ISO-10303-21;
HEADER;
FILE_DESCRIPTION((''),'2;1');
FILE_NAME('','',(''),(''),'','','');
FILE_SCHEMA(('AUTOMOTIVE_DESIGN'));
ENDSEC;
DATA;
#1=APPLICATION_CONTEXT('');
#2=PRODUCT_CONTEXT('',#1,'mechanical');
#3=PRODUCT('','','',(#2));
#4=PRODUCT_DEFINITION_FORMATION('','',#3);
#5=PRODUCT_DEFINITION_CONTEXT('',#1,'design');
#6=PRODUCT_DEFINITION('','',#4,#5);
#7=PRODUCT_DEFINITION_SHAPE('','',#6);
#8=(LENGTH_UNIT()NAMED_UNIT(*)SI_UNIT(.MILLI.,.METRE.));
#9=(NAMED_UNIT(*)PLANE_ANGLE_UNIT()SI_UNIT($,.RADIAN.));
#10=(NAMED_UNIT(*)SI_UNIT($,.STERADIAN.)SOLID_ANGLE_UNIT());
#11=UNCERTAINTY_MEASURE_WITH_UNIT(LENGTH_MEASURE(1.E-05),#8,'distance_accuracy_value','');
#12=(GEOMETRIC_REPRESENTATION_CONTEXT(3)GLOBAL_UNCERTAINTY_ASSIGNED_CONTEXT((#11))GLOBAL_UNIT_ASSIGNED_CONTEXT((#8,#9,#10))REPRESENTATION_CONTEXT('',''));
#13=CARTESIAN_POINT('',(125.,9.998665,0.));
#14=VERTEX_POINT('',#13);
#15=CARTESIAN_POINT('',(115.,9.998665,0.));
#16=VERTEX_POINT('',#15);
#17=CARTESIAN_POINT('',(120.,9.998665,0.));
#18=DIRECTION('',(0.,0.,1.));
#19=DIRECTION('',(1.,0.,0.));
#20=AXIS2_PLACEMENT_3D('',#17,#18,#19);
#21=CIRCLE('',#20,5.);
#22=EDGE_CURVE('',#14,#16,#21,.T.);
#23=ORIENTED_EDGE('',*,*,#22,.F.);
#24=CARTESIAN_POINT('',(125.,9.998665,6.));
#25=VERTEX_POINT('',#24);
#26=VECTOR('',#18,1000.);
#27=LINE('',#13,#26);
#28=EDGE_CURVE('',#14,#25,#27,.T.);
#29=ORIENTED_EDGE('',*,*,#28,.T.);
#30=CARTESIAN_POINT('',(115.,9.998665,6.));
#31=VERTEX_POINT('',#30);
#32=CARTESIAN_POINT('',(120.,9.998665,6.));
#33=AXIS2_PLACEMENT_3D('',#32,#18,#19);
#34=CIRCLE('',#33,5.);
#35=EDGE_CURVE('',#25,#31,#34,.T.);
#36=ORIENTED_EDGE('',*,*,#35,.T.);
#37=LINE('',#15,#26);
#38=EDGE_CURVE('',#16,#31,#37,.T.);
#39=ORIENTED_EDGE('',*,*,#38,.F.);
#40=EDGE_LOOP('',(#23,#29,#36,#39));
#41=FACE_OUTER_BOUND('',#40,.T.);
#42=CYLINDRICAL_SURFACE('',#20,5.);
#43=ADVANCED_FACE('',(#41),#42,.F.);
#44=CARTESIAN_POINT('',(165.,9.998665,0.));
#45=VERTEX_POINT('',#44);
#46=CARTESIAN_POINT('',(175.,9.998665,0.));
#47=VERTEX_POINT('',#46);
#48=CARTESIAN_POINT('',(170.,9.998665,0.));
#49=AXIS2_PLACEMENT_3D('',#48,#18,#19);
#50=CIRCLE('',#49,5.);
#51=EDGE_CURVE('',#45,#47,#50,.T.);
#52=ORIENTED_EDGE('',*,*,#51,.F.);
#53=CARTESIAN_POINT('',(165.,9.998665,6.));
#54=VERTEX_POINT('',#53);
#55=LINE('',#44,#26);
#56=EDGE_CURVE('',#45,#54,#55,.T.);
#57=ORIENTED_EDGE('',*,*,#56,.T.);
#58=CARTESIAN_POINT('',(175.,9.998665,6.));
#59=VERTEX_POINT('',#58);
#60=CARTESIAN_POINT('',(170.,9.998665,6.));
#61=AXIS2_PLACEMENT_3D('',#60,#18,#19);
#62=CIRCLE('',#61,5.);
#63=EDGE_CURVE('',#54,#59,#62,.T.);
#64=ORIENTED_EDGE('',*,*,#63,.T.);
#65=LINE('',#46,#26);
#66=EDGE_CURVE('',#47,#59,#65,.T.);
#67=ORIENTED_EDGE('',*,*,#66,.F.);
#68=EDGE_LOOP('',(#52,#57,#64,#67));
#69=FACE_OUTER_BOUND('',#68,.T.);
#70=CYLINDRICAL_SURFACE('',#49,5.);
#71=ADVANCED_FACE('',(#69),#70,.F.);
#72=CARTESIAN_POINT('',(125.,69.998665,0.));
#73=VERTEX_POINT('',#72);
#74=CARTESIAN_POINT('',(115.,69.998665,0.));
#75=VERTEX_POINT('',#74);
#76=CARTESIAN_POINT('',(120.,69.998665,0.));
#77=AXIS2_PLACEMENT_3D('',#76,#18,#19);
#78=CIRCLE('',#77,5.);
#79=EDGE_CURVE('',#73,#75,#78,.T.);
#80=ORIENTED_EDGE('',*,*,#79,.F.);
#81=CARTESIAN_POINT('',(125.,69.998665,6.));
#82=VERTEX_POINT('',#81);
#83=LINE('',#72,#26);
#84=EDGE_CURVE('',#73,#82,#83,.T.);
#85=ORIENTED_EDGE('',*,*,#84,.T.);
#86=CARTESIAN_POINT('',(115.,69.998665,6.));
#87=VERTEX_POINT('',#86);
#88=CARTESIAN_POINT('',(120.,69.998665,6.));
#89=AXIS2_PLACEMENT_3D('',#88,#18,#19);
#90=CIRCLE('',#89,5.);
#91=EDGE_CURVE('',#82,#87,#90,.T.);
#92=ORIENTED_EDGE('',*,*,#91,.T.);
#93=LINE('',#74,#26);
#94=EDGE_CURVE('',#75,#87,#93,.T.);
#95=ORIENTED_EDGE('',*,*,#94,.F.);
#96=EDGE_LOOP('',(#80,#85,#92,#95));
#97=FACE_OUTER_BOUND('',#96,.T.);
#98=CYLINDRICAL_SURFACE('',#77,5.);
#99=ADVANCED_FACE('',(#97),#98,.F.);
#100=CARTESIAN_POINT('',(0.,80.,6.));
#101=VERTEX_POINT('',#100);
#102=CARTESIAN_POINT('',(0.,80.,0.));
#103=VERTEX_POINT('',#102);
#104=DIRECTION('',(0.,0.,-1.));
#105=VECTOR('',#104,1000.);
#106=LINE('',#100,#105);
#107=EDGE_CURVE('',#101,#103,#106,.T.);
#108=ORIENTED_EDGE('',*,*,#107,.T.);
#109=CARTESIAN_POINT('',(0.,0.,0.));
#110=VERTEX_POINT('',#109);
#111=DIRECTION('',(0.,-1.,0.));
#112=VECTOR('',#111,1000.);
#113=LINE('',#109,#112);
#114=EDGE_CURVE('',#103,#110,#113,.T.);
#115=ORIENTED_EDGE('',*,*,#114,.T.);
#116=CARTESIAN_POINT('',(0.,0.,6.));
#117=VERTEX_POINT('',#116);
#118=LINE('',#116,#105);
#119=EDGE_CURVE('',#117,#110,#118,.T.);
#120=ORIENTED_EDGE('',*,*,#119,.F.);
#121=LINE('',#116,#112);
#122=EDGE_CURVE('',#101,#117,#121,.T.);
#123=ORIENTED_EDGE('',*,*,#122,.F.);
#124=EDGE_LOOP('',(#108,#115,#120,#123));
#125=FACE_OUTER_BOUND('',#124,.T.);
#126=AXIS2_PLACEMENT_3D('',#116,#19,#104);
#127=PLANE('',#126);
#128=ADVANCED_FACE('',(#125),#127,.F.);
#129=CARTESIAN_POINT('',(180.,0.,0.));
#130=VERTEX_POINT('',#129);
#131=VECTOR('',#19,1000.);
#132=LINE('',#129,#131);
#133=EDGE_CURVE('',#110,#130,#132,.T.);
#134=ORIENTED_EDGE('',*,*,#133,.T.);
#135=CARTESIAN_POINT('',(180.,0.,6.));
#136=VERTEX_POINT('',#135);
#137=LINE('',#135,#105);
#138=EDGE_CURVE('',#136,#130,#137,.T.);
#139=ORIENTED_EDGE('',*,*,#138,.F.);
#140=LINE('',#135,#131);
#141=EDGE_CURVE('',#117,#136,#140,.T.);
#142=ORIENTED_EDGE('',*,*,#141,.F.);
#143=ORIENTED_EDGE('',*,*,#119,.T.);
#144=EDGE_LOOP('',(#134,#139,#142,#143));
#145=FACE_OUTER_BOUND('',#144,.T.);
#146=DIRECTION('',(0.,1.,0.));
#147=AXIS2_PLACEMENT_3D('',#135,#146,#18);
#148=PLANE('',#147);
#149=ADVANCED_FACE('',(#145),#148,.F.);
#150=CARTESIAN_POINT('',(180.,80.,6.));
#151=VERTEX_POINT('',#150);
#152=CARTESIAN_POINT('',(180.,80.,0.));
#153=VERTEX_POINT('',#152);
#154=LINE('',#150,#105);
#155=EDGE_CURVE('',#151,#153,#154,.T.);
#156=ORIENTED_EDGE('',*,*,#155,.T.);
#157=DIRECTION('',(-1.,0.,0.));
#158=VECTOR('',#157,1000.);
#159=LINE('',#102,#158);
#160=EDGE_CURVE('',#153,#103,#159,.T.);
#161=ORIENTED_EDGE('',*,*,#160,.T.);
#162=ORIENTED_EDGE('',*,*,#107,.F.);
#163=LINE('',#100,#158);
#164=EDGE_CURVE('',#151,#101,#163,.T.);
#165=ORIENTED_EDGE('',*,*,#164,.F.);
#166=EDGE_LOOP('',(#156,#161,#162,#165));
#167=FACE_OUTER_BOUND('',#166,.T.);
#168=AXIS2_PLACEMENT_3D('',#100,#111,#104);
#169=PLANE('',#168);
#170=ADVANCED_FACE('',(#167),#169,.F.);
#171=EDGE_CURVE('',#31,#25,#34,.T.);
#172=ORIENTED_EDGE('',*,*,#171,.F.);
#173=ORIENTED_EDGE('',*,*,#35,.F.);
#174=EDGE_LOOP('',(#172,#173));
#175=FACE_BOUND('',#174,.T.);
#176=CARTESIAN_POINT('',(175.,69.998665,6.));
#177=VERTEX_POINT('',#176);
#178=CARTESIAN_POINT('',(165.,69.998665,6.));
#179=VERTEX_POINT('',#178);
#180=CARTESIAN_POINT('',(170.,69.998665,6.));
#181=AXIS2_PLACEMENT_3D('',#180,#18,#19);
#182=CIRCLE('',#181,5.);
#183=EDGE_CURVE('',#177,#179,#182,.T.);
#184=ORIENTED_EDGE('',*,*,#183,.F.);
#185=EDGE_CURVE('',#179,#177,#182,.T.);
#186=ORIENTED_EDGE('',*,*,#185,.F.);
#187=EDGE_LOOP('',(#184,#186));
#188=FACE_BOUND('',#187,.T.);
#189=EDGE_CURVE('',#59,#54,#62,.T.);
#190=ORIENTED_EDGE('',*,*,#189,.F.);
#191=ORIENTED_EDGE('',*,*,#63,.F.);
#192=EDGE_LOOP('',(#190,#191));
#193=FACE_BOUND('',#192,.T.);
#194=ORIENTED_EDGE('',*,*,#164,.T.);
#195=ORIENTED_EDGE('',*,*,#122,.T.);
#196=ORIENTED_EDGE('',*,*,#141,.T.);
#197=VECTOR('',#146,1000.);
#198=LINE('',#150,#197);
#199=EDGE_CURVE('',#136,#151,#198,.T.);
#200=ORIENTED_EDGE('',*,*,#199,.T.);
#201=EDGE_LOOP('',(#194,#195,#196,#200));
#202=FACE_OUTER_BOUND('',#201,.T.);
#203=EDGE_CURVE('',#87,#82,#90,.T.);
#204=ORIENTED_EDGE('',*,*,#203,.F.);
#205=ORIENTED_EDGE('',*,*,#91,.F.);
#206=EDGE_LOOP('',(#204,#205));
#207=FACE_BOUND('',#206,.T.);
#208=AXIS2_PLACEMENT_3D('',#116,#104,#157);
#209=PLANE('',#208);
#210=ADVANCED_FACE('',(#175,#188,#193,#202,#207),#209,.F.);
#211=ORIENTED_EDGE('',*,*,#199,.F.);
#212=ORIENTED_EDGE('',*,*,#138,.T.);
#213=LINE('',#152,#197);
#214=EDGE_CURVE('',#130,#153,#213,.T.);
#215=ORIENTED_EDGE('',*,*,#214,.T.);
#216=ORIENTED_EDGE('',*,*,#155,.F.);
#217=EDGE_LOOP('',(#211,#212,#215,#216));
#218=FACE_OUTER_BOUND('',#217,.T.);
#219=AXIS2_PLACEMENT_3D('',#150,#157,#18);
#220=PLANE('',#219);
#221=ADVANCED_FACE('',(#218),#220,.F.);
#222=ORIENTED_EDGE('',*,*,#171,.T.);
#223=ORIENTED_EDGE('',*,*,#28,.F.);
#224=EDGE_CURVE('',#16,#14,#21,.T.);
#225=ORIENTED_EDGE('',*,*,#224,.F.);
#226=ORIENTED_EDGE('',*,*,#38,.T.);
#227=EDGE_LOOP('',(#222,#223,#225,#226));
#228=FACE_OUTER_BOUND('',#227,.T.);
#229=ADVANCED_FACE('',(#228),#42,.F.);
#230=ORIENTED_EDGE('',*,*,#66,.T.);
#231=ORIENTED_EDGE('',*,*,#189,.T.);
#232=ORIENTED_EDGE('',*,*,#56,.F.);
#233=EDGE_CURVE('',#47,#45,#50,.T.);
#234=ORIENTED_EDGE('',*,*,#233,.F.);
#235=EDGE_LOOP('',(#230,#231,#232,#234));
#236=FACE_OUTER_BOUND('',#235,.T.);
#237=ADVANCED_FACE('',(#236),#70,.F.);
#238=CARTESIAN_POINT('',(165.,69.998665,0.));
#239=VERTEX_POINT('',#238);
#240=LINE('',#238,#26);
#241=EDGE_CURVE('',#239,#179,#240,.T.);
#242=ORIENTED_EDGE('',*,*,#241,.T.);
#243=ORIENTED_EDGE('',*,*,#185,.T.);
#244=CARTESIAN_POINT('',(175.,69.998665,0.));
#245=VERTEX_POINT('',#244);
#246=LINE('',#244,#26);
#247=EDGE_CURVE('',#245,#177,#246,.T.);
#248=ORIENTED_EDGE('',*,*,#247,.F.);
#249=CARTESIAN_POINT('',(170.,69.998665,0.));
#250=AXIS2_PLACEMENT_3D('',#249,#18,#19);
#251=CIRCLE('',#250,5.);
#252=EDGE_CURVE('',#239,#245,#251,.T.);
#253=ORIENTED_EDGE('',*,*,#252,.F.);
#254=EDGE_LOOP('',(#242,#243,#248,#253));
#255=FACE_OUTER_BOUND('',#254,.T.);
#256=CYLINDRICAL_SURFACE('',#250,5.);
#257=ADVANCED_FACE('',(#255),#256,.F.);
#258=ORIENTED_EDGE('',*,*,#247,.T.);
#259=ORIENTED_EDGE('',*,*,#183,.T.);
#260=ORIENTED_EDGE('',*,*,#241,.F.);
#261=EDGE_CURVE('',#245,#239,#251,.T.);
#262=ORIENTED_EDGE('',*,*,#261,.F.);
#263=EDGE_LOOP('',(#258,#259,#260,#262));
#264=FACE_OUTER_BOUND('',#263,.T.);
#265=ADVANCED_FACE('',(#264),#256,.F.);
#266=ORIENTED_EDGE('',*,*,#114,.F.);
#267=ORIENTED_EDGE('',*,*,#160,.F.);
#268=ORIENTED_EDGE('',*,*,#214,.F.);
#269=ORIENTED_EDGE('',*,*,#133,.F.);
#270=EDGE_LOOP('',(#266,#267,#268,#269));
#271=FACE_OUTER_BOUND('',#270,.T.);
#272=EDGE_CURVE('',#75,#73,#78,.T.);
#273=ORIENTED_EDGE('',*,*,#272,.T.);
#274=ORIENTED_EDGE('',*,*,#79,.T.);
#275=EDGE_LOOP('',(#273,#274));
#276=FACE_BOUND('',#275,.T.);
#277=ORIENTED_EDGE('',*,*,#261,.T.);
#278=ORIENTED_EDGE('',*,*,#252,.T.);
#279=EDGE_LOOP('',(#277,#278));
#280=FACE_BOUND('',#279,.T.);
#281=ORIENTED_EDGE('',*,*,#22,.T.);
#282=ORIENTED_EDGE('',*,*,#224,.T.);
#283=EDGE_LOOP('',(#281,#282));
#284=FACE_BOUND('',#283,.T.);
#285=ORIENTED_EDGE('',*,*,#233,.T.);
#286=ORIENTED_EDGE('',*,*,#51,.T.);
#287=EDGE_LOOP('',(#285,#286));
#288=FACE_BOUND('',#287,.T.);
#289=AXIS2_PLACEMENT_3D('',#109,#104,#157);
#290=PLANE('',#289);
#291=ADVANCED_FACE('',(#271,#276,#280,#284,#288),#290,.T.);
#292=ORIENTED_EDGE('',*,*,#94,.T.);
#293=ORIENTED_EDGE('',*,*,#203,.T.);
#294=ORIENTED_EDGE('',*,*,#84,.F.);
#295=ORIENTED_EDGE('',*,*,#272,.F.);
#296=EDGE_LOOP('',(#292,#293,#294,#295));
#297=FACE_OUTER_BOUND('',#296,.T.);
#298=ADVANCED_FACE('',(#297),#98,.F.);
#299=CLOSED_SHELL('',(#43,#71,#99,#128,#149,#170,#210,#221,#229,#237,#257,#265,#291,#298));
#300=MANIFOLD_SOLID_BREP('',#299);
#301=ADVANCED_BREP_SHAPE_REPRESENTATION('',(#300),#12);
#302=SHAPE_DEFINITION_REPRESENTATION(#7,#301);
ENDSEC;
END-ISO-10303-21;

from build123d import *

# Parameters (mm, degrees)
SKETCH_1_W          = 180
SKETCH_1_H          = 80
EXTRUDE_1_DEPTH     = 6
SKETCH_2_R          = 5
CUT_EXTRUDE_1_DEPTH = 6


with BuildPart() as part:
    # 草图1 → 凸台-拉伸1 (new body)
    with BuildSketch(Plane.XY):
        with Locations((90, 40)):
            Rectangle(SKETCH_1_W, SKETCH_1_H)
    extrude(amount=EXTRUDE_1_DEPTH)

    # 草图2 → 切除-拉伸1 (cut)
    with BuildSketch(Plane.XY.offset(6)):
        with Locations((170, 69.998664645)):
            Circle(SKETCH_2_R)
        with Locations((120, 9.998664645)):
            Circle(SKETCH_2_R)
        with Locations((120, 69.998664645)):
            Circle(SKETCH_2_R)
        with Locations((170, 9.998664645)):
            Circle(SKETCH_2_R)
    extrude(amount=-CUT_EXTRUDE_1_DEPTH, mode=Mode.SUBTRACT)


solid = part.part
